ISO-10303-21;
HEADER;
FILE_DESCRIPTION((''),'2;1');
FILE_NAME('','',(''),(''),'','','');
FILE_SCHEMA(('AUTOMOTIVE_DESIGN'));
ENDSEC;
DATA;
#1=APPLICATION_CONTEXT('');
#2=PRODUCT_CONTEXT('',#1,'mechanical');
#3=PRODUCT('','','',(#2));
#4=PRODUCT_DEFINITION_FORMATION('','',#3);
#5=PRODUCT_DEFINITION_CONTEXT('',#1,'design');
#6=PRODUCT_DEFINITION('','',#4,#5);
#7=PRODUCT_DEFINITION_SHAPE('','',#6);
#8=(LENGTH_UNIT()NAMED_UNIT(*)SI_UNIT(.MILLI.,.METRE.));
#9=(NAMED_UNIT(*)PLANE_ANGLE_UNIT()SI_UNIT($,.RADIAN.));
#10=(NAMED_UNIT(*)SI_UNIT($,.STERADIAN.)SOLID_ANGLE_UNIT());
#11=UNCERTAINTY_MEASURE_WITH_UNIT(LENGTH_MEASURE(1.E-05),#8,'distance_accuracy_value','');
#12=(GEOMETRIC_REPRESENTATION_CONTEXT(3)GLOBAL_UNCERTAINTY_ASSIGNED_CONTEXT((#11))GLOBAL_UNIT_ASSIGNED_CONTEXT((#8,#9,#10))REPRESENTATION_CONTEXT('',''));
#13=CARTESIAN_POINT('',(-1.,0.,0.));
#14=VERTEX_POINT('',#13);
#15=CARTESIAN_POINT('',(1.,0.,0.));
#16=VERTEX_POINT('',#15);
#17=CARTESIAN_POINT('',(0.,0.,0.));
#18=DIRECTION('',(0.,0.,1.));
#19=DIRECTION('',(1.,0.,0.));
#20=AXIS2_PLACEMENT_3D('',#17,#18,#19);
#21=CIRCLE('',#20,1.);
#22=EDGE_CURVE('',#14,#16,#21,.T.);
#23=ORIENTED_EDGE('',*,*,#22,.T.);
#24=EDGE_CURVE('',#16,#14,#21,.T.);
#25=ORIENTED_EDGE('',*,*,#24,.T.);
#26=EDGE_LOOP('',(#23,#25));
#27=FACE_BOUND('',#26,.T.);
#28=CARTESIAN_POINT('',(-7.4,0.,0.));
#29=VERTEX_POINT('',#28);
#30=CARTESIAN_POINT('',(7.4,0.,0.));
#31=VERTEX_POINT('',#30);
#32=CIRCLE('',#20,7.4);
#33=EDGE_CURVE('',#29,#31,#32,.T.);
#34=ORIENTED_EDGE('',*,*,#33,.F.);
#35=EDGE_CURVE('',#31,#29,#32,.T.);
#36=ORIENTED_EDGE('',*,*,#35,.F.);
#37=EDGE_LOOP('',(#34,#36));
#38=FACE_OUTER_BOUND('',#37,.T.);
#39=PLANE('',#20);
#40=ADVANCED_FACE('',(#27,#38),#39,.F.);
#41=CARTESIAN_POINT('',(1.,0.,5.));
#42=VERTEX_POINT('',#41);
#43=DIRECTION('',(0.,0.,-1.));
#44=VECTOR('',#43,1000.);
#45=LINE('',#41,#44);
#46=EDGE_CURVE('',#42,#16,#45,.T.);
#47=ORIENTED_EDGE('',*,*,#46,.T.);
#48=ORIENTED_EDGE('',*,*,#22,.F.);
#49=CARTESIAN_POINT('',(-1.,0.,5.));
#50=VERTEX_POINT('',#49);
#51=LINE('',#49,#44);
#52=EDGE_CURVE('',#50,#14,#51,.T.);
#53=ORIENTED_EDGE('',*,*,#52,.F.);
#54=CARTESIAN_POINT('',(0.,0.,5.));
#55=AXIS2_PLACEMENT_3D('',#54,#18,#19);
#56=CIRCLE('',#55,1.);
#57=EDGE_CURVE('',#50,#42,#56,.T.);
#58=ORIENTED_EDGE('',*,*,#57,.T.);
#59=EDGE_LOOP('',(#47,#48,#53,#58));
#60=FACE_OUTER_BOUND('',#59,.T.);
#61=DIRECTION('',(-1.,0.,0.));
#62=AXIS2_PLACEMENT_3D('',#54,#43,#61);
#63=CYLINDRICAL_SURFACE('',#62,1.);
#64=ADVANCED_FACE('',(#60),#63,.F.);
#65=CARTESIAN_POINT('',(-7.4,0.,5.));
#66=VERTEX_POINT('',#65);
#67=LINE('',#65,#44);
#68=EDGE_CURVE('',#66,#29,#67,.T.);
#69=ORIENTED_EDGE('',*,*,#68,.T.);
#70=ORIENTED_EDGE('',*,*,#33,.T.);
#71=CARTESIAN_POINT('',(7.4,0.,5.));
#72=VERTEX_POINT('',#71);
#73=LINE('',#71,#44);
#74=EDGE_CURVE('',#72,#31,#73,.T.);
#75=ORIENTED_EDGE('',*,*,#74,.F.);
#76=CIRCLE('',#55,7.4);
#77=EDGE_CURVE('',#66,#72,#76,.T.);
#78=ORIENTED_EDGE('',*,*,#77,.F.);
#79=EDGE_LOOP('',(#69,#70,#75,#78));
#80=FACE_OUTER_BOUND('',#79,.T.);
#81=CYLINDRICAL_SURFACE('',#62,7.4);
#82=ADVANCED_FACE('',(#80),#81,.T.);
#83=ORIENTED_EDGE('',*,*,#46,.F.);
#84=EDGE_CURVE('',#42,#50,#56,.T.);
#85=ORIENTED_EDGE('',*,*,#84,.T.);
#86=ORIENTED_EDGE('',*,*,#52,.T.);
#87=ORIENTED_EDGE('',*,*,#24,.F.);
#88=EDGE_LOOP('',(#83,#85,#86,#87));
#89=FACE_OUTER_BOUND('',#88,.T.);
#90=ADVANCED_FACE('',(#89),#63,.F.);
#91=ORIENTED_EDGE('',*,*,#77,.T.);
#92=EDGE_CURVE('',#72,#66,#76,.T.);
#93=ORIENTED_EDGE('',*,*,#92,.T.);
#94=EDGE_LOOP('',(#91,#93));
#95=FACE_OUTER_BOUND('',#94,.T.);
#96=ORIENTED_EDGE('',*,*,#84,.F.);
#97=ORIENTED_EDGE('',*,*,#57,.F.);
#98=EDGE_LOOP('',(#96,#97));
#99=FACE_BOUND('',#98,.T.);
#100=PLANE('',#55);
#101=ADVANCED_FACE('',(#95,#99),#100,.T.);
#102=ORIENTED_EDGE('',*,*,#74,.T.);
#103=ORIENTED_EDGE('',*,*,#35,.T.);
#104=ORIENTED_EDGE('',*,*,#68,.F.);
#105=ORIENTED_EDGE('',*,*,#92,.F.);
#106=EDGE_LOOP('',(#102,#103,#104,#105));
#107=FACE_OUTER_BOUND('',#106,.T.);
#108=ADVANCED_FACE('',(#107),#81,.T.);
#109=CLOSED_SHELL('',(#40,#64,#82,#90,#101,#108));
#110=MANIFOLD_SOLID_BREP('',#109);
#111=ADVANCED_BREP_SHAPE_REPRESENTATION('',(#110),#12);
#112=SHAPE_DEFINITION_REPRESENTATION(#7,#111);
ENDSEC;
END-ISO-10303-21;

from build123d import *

# Parameters (mm, degrees)
SKETCH1_R           = 7.4
SKETCH1_R_2         = 1
BOSS_EXTRUDE1_DEPTH = 5


with BuildPart() as part:
    # Sketch1 → Boss-Extrude1 (new body)
    with BuildSketch(Plane.XY):
        Circle(SKETCH1_R)
        Circle(SKETCH1_R_2, mode=Mode.SUBTRACT)
    extrude(amount=BOSS_EXTRUDE1_DEPTH)


solid = part.part
